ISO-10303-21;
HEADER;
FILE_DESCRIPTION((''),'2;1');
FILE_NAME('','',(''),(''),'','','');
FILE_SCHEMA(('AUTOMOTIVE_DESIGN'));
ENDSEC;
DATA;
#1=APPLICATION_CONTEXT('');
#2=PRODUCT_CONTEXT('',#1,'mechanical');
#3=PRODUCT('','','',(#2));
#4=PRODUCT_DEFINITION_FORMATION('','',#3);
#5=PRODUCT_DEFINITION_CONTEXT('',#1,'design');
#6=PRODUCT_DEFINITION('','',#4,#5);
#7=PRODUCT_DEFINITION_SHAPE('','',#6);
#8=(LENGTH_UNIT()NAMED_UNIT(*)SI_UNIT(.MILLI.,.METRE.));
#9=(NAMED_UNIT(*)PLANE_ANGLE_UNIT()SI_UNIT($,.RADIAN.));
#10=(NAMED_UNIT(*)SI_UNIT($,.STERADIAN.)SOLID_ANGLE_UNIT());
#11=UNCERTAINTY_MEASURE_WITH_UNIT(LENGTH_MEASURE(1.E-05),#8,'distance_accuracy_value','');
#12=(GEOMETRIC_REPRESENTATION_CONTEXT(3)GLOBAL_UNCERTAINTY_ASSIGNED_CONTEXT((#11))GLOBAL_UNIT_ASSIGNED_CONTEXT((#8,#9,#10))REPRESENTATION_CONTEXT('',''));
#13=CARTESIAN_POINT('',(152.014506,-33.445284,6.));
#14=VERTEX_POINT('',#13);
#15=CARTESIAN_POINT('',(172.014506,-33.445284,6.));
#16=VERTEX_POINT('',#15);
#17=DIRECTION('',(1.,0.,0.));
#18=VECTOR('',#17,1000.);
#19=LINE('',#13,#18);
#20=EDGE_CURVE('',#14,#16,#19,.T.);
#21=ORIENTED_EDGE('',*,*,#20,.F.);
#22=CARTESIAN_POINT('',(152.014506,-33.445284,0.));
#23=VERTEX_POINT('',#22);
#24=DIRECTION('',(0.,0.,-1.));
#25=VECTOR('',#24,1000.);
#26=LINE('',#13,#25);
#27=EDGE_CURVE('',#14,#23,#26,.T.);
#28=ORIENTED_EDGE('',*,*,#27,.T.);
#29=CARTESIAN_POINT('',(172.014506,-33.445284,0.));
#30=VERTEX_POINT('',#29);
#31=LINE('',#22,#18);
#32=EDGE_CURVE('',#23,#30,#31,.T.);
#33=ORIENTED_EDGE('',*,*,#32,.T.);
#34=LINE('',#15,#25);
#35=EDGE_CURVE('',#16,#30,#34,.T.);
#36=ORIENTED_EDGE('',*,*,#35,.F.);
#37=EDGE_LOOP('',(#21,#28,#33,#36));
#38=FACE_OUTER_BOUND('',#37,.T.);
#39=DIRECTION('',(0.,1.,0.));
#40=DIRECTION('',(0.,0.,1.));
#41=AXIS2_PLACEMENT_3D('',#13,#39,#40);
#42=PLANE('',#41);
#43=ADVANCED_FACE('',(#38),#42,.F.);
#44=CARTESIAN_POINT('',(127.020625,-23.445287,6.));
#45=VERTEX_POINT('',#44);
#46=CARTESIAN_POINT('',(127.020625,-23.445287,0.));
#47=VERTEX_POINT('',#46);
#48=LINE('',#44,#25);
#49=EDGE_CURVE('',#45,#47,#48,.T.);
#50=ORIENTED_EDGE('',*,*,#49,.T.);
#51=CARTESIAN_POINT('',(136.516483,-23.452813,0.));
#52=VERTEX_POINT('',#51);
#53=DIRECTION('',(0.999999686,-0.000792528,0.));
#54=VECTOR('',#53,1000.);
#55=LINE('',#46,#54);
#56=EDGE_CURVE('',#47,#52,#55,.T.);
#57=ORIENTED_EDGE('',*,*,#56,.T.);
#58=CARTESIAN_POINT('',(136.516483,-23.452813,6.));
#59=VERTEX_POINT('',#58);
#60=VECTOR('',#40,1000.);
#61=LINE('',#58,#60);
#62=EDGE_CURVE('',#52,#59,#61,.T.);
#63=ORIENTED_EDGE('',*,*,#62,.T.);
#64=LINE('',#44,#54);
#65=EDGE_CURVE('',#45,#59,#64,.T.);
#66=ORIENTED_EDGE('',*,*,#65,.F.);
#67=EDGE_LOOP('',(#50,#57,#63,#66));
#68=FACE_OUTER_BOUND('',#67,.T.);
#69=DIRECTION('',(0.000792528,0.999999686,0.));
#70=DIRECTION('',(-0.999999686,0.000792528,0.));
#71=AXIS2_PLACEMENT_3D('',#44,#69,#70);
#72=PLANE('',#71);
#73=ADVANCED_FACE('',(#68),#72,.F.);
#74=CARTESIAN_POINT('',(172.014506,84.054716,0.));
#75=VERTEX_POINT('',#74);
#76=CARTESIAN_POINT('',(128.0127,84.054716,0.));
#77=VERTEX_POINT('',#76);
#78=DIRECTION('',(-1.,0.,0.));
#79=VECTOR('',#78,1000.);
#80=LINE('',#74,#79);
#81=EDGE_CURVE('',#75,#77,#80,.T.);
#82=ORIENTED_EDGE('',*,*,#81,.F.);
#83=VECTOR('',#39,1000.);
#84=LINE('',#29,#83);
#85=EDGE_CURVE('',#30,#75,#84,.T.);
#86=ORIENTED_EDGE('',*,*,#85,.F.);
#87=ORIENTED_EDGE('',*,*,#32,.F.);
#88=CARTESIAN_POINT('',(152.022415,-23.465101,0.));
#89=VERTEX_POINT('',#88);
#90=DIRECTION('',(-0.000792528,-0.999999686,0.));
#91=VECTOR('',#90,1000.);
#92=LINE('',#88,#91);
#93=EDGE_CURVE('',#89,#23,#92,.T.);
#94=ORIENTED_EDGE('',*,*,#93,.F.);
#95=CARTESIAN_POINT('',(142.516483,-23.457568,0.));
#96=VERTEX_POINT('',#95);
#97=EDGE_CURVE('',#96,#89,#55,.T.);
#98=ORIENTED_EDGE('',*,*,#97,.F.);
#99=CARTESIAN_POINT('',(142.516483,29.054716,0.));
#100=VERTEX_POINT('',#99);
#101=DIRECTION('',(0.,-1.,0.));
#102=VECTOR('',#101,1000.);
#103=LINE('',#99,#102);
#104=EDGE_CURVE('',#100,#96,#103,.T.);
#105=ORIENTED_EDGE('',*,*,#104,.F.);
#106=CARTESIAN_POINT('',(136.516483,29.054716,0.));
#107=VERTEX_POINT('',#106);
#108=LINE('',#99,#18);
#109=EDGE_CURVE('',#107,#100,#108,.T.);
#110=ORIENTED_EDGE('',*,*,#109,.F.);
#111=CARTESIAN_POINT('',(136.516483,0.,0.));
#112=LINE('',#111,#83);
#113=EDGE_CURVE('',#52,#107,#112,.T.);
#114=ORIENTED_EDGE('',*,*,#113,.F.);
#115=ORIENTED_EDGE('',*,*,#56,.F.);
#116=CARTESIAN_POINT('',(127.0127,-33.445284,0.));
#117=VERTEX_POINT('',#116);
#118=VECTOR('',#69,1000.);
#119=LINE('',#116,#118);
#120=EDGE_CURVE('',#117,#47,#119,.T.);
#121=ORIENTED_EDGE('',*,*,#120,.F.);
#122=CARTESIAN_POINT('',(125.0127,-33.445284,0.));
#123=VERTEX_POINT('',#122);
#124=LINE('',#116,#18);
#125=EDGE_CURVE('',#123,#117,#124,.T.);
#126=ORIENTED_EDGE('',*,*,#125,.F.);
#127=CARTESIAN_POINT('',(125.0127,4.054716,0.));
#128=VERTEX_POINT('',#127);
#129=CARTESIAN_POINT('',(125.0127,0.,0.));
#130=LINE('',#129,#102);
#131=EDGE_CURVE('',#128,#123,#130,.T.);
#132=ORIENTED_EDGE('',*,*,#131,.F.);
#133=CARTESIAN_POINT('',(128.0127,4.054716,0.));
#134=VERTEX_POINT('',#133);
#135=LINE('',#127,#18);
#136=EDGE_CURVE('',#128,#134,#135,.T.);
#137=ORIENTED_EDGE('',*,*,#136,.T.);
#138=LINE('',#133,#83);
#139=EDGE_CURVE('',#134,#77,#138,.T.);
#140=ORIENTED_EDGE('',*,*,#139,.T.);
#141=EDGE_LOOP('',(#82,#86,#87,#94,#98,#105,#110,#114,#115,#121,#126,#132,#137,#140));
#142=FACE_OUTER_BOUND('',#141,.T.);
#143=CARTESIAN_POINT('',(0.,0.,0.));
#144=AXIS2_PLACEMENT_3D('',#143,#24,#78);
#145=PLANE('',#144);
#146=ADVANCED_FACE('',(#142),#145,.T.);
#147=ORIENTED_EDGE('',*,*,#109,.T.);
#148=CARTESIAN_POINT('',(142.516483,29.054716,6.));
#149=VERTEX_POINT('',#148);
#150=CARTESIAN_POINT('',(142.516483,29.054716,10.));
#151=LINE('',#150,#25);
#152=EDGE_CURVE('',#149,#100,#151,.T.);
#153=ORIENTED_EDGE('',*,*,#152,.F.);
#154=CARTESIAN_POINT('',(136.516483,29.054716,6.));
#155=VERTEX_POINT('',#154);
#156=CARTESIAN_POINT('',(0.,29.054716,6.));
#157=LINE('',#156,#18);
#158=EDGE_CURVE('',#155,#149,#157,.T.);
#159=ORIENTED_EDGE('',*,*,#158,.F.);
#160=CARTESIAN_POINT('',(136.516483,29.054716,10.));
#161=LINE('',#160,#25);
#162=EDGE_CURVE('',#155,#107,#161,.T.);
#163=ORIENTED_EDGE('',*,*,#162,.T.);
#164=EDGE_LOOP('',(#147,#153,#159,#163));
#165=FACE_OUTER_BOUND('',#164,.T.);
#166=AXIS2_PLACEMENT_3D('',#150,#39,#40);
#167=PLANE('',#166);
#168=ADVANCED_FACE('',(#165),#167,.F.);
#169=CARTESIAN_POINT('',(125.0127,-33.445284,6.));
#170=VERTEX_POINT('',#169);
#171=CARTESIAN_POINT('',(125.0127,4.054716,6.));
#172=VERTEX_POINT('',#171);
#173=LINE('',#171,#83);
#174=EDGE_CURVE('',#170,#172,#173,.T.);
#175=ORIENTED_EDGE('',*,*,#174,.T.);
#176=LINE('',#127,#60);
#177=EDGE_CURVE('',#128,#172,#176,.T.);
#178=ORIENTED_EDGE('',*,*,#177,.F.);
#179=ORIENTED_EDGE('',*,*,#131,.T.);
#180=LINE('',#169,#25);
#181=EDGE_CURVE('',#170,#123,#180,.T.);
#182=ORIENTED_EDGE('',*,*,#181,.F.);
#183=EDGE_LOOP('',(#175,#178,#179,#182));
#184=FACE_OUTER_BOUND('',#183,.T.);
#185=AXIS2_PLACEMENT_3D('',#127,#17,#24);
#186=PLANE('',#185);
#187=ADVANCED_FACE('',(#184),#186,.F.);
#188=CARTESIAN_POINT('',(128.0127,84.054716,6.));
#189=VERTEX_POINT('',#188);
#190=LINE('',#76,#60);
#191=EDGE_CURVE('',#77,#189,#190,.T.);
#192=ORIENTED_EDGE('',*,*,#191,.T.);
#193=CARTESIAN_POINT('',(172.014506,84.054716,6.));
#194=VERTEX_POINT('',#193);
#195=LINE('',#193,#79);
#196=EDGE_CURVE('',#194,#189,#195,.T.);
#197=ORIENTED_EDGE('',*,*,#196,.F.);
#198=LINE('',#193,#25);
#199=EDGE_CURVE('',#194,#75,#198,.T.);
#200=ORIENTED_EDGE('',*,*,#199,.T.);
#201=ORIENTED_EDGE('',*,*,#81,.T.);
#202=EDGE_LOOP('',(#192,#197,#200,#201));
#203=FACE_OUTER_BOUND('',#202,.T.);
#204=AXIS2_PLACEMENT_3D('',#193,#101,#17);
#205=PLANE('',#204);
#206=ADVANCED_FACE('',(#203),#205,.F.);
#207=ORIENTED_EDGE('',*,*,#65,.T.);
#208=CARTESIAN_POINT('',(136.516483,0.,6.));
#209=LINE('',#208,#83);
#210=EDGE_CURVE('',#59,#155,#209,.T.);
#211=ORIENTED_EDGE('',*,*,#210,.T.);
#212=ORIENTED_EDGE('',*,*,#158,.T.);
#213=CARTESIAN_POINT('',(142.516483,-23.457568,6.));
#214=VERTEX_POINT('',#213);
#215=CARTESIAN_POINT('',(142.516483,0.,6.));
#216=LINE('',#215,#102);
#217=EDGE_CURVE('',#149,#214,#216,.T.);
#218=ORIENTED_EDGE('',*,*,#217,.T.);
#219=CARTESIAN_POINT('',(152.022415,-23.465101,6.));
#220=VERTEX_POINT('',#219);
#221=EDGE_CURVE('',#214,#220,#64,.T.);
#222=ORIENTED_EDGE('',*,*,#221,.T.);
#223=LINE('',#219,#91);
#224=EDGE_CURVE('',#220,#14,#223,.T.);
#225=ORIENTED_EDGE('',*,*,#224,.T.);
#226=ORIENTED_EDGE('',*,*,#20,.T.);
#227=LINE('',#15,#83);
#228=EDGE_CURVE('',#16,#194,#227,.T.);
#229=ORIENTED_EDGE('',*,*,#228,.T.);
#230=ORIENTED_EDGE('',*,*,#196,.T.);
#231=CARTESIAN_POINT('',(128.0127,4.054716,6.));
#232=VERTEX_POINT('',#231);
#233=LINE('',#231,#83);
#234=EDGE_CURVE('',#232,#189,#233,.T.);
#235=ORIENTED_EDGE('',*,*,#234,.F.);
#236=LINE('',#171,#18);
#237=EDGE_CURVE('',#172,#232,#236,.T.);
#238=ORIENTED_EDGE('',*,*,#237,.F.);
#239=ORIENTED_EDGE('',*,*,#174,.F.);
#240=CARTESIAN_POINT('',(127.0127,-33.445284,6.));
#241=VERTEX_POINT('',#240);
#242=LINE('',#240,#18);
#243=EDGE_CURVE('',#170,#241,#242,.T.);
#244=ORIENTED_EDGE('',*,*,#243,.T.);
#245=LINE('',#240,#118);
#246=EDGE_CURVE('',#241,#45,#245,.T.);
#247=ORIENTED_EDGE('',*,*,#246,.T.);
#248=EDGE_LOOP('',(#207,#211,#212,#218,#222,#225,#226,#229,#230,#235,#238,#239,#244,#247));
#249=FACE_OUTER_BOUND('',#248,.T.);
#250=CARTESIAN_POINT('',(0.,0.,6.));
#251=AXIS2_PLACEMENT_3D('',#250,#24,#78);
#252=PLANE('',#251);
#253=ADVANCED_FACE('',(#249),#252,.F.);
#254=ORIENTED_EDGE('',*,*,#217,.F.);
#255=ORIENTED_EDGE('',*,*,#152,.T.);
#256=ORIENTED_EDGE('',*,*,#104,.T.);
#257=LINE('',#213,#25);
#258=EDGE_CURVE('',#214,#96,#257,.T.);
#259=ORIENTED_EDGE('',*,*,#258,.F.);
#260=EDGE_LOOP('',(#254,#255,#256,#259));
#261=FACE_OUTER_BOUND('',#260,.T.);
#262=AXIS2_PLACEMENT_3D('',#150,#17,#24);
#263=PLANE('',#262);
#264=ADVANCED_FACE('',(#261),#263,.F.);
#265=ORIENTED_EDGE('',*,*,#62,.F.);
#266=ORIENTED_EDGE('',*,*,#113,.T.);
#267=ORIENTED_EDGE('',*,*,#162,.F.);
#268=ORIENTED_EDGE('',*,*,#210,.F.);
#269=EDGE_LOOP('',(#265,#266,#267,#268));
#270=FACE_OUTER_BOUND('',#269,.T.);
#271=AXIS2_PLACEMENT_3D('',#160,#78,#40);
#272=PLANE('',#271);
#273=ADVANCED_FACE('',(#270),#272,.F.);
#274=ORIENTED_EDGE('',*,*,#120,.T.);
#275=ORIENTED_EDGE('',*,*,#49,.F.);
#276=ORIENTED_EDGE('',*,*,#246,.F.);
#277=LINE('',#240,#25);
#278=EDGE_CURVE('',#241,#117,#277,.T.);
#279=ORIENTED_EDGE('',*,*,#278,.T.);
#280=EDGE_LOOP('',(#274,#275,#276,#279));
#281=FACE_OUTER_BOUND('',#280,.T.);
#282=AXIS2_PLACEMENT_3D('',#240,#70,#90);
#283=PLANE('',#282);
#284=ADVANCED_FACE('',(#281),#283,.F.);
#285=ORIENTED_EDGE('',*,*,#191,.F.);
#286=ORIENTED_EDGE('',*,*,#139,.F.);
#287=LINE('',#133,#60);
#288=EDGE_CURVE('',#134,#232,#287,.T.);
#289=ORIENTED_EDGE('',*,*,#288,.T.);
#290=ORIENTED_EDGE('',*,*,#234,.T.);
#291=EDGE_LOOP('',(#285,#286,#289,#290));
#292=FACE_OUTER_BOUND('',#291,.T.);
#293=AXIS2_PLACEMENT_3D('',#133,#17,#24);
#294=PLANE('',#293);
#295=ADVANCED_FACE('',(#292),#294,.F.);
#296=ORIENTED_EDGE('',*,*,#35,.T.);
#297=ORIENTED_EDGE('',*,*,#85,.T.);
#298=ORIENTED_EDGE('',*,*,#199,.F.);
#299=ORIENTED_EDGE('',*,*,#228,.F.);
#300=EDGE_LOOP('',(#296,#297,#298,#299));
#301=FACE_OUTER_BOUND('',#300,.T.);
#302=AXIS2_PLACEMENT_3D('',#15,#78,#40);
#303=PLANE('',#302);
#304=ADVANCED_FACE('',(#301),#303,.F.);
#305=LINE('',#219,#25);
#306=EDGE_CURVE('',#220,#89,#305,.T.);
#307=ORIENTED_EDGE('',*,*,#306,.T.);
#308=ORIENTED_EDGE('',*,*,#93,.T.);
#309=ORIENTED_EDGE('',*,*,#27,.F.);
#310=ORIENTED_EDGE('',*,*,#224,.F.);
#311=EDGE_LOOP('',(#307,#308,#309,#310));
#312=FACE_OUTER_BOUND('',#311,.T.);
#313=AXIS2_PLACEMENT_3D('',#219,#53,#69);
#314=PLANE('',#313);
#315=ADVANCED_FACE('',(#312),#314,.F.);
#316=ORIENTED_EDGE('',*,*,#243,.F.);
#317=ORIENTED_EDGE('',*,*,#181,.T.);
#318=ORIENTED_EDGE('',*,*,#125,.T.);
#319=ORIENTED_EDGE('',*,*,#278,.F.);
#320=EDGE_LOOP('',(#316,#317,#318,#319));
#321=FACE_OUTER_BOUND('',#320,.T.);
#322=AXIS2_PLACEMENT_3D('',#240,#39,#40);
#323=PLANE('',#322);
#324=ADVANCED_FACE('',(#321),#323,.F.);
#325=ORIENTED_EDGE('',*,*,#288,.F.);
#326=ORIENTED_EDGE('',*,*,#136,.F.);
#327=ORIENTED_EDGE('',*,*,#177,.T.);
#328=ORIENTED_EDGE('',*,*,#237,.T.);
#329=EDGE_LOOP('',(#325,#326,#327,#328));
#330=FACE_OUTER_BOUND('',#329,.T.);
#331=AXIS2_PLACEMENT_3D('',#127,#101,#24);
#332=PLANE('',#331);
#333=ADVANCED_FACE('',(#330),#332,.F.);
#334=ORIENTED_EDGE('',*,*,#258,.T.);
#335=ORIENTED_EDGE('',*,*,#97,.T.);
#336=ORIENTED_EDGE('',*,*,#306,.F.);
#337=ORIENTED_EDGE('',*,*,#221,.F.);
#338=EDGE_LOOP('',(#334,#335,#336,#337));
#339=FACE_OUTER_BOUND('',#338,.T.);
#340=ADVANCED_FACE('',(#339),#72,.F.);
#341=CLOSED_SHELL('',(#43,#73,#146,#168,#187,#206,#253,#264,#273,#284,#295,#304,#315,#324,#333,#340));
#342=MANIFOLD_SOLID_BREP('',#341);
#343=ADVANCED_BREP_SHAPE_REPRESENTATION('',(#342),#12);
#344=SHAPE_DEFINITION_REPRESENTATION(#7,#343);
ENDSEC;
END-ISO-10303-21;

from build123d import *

# Parameters (mm, degrees)
BOSS_EXTRUDE1_DEPTH = 6
SKETCH3_W           = 6
SKETCH3_H           = 60
CUT_EXTRUDE1_DEPTH  = 10
CUT_EXTRUDE2_DEPTH  = 192.546823128


with BuildPart() as part:
    # Sketch1 → Boss-Extrude1 (new body)
    with BuildSketch(Plane.XY):
        Polygon((127.012699858, -33.445283653), (107.012699858, -33.445283653), (107.012699858, 84.054716347), (172.014505523, 84.054716347), (172.014505523, -33.445283653), (152.014505523, -33.445283653), (152.022415095, -23.465101408), (127.020625134, -23.445286794), align=None)
    extrude(amount=BOSS_EXTRUDE1_DEPTH)

    # Sketch3 → Cut-Extrude1 (cut)
    with BuildSketch(Plane(origin=(0, 0, 0), x_dir=(-1, 0, 0), z_dir=(0, 0, -1))):
        with Locations((-139.516482917, -0.945283653)):
            Rectangle(SKETCH3_W, SKETCH3_H)
    extrude(amount=-CUT_EXTRUDE1_DEPTH, mode=Mode.SUBTRACT)

    # Sketch4 → Cut-Extrude2 (cut, through all)
    with BuildSketch(Plane.XY.offset(6)):
        Polygon((125.012699858, -36.580409203), (107.012699858, -36.580409203), (107.012699858, 84.054716347), (128.012699858, 84.054716347), (128.012699858, 4.054716347), (125.012699858, 4.054716347), align=None)
    extrude(amount=-CUT_EXTRUDE2_DEPTH, mode=Mode.SUBTRACT)


solid = part.part
